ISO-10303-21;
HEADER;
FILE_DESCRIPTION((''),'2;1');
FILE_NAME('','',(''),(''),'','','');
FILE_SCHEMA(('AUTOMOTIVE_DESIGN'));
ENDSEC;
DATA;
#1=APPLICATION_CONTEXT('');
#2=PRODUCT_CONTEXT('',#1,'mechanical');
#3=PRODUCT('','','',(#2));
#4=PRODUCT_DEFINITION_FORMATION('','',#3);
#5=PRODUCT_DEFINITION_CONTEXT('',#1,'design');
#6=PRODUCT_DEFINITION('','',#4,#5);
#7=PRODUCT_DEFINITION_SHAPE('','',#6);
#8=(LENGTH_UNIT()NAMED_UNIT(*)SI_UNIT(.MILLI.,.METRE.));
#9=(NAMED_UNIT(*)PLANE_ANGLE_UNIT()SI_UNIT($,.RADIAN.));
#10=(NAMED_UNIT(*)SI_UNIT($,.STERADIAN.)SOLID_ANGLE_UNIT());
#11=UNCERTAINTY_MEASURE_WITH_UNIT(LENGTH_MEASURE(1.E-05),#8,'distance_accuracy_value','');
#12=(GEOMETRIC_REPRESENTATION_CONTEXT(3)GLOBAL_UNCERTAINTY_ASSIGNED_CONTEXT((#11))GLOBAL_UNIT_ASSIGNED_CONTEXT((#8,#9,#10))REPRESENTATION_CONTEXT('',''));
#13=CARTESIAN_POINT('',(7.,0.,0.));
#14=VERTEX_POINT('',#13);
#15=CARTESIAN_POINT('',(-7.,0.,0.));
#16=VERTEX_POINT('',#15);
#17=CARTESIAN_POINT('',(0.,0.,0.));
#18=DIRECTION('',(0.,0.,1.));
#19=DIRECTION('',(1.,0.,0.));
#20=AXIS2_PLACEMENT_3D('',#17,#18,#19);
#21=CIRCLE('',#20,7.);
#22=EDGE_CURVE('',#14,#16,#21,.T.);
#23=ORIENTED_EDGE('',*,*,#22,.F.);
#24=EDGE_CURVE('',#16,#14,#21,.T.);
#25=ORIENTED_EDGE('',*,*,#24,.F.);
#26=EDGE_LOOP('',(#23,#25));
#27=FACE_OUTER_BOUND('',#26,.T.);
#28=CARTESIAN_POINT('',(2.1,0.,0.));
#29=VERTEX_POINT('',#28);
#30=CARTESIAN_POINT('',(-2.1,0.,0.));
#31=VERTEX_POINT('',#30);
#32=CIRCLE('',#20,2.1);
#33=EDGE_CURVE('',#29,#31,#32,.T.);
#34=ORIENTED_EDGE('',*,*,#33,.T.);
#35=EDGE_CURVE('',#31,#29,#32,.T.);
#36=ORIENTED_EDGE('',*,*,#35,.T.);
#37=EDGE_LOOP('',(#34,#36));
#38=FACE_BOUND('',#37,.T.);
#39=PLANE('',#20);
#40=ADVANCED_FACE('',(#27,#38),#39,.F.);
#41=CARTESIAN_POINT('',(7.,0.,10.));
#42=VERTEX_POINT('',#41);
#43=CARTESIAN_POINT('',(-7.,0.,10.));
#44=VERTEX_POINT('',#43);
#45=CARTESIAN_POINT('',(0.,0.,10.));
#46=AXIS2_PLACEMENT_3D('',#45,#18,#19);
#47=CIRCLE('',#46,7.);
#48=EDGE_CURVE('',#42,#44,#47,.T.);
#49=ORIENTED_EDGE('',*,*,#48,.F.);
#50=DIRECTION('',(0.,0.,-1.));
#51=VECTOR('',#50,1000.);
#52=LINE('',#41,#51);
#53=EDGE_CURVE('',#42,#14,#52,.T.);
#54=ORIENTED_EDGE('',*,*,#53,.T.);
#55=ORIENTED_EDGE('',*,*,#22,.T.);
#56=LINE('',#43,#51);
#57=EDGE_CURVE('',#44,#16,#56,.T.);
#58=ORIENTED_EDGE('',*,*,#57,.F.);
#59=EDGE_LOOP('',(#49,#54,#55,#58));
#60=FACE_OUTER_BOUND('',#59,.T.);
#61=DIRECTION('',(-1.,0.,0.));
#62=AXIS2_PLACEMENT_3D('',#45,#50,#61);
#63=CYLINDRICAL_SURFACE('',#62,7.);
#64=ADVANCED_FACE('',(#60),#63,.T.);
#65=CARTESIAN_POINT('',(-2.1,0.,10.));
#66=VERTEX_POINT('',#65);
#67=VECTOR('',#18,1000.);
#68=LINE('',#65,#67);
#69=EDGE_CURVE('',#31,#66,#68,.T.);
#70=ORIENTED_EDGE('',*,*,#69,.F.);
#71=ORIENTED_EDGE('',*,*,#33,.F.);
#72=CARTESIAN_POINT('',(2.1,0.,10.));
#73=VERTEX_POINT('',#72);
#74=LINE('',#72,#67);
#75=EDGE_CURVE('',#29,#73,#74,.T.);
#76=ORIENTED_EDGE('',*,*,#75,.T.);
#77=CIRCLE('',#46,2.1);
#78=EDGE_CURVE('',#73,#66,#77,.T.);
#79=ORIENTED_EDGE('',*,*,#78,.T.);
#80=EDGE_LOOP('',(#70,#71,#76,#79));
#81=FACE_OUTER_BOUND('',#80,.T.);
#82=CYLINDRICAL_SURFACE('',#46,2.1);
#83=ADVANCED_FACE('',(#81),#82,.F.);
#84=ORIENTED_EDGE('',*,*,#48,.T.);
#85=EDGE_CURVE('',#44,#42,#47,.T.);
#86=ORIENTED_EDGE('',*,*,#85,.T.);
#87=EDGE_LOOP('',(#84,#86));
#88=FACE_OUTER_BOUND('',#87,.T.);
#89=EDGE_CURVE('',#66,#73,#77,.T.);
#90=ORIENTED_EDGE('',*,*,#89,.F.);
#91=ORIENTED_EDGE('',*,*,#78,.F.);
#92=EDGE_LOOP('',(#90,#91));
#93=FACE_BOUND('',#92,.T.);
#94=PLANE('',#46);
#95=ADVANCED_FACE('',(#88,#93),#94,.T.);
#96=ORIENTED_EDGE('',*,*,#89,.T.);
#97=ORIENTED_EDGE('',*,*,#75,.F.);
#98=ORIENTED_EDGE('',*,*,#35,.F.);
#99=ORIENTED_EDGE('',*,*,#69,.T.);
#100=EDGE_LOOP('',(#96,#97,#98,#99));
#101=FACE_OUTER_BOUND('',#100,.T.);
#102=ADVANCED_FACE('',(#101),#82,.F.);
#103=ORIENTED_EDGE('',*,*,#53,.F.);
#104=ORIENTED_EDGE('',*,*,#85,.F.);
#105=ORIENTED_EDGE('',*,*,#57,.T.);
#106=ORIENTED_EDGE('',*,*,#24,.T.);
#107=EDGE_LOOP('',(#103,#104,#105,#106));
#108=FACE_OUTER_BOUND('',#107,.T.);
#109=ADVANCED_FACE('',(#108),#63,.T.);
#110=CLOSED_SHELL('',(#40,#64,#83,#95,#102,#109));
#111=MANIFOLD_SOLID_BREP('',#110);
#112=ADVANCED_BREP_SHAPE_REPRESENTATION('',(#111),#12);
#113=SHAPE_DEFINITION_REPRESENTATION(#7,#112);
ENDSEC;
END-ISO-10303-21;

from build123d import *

# Parameters (mm, degrees)
SKETCH_1_R         = 7
EXTRUDE_1_DEPTH    = 10
HOLE_WIZARD_M5_1_D = 4.2


with BuildPart() as part:
    # 草图1 → 凸台-拉伸1 (new body)
    with BuildSketch(Plane.XY):
        Circle(SKETCH_1_R)
    extrude(amount=EXTRUDE_1_DEPTH)

    # M5 螺纹孔1 (through all)
    with Locations(Plane.XY.offset(10)):
        with Locations((0, 0)):
            Hole(HOLE_WIZARD_M5_1_D / 2)


solid = part.part
